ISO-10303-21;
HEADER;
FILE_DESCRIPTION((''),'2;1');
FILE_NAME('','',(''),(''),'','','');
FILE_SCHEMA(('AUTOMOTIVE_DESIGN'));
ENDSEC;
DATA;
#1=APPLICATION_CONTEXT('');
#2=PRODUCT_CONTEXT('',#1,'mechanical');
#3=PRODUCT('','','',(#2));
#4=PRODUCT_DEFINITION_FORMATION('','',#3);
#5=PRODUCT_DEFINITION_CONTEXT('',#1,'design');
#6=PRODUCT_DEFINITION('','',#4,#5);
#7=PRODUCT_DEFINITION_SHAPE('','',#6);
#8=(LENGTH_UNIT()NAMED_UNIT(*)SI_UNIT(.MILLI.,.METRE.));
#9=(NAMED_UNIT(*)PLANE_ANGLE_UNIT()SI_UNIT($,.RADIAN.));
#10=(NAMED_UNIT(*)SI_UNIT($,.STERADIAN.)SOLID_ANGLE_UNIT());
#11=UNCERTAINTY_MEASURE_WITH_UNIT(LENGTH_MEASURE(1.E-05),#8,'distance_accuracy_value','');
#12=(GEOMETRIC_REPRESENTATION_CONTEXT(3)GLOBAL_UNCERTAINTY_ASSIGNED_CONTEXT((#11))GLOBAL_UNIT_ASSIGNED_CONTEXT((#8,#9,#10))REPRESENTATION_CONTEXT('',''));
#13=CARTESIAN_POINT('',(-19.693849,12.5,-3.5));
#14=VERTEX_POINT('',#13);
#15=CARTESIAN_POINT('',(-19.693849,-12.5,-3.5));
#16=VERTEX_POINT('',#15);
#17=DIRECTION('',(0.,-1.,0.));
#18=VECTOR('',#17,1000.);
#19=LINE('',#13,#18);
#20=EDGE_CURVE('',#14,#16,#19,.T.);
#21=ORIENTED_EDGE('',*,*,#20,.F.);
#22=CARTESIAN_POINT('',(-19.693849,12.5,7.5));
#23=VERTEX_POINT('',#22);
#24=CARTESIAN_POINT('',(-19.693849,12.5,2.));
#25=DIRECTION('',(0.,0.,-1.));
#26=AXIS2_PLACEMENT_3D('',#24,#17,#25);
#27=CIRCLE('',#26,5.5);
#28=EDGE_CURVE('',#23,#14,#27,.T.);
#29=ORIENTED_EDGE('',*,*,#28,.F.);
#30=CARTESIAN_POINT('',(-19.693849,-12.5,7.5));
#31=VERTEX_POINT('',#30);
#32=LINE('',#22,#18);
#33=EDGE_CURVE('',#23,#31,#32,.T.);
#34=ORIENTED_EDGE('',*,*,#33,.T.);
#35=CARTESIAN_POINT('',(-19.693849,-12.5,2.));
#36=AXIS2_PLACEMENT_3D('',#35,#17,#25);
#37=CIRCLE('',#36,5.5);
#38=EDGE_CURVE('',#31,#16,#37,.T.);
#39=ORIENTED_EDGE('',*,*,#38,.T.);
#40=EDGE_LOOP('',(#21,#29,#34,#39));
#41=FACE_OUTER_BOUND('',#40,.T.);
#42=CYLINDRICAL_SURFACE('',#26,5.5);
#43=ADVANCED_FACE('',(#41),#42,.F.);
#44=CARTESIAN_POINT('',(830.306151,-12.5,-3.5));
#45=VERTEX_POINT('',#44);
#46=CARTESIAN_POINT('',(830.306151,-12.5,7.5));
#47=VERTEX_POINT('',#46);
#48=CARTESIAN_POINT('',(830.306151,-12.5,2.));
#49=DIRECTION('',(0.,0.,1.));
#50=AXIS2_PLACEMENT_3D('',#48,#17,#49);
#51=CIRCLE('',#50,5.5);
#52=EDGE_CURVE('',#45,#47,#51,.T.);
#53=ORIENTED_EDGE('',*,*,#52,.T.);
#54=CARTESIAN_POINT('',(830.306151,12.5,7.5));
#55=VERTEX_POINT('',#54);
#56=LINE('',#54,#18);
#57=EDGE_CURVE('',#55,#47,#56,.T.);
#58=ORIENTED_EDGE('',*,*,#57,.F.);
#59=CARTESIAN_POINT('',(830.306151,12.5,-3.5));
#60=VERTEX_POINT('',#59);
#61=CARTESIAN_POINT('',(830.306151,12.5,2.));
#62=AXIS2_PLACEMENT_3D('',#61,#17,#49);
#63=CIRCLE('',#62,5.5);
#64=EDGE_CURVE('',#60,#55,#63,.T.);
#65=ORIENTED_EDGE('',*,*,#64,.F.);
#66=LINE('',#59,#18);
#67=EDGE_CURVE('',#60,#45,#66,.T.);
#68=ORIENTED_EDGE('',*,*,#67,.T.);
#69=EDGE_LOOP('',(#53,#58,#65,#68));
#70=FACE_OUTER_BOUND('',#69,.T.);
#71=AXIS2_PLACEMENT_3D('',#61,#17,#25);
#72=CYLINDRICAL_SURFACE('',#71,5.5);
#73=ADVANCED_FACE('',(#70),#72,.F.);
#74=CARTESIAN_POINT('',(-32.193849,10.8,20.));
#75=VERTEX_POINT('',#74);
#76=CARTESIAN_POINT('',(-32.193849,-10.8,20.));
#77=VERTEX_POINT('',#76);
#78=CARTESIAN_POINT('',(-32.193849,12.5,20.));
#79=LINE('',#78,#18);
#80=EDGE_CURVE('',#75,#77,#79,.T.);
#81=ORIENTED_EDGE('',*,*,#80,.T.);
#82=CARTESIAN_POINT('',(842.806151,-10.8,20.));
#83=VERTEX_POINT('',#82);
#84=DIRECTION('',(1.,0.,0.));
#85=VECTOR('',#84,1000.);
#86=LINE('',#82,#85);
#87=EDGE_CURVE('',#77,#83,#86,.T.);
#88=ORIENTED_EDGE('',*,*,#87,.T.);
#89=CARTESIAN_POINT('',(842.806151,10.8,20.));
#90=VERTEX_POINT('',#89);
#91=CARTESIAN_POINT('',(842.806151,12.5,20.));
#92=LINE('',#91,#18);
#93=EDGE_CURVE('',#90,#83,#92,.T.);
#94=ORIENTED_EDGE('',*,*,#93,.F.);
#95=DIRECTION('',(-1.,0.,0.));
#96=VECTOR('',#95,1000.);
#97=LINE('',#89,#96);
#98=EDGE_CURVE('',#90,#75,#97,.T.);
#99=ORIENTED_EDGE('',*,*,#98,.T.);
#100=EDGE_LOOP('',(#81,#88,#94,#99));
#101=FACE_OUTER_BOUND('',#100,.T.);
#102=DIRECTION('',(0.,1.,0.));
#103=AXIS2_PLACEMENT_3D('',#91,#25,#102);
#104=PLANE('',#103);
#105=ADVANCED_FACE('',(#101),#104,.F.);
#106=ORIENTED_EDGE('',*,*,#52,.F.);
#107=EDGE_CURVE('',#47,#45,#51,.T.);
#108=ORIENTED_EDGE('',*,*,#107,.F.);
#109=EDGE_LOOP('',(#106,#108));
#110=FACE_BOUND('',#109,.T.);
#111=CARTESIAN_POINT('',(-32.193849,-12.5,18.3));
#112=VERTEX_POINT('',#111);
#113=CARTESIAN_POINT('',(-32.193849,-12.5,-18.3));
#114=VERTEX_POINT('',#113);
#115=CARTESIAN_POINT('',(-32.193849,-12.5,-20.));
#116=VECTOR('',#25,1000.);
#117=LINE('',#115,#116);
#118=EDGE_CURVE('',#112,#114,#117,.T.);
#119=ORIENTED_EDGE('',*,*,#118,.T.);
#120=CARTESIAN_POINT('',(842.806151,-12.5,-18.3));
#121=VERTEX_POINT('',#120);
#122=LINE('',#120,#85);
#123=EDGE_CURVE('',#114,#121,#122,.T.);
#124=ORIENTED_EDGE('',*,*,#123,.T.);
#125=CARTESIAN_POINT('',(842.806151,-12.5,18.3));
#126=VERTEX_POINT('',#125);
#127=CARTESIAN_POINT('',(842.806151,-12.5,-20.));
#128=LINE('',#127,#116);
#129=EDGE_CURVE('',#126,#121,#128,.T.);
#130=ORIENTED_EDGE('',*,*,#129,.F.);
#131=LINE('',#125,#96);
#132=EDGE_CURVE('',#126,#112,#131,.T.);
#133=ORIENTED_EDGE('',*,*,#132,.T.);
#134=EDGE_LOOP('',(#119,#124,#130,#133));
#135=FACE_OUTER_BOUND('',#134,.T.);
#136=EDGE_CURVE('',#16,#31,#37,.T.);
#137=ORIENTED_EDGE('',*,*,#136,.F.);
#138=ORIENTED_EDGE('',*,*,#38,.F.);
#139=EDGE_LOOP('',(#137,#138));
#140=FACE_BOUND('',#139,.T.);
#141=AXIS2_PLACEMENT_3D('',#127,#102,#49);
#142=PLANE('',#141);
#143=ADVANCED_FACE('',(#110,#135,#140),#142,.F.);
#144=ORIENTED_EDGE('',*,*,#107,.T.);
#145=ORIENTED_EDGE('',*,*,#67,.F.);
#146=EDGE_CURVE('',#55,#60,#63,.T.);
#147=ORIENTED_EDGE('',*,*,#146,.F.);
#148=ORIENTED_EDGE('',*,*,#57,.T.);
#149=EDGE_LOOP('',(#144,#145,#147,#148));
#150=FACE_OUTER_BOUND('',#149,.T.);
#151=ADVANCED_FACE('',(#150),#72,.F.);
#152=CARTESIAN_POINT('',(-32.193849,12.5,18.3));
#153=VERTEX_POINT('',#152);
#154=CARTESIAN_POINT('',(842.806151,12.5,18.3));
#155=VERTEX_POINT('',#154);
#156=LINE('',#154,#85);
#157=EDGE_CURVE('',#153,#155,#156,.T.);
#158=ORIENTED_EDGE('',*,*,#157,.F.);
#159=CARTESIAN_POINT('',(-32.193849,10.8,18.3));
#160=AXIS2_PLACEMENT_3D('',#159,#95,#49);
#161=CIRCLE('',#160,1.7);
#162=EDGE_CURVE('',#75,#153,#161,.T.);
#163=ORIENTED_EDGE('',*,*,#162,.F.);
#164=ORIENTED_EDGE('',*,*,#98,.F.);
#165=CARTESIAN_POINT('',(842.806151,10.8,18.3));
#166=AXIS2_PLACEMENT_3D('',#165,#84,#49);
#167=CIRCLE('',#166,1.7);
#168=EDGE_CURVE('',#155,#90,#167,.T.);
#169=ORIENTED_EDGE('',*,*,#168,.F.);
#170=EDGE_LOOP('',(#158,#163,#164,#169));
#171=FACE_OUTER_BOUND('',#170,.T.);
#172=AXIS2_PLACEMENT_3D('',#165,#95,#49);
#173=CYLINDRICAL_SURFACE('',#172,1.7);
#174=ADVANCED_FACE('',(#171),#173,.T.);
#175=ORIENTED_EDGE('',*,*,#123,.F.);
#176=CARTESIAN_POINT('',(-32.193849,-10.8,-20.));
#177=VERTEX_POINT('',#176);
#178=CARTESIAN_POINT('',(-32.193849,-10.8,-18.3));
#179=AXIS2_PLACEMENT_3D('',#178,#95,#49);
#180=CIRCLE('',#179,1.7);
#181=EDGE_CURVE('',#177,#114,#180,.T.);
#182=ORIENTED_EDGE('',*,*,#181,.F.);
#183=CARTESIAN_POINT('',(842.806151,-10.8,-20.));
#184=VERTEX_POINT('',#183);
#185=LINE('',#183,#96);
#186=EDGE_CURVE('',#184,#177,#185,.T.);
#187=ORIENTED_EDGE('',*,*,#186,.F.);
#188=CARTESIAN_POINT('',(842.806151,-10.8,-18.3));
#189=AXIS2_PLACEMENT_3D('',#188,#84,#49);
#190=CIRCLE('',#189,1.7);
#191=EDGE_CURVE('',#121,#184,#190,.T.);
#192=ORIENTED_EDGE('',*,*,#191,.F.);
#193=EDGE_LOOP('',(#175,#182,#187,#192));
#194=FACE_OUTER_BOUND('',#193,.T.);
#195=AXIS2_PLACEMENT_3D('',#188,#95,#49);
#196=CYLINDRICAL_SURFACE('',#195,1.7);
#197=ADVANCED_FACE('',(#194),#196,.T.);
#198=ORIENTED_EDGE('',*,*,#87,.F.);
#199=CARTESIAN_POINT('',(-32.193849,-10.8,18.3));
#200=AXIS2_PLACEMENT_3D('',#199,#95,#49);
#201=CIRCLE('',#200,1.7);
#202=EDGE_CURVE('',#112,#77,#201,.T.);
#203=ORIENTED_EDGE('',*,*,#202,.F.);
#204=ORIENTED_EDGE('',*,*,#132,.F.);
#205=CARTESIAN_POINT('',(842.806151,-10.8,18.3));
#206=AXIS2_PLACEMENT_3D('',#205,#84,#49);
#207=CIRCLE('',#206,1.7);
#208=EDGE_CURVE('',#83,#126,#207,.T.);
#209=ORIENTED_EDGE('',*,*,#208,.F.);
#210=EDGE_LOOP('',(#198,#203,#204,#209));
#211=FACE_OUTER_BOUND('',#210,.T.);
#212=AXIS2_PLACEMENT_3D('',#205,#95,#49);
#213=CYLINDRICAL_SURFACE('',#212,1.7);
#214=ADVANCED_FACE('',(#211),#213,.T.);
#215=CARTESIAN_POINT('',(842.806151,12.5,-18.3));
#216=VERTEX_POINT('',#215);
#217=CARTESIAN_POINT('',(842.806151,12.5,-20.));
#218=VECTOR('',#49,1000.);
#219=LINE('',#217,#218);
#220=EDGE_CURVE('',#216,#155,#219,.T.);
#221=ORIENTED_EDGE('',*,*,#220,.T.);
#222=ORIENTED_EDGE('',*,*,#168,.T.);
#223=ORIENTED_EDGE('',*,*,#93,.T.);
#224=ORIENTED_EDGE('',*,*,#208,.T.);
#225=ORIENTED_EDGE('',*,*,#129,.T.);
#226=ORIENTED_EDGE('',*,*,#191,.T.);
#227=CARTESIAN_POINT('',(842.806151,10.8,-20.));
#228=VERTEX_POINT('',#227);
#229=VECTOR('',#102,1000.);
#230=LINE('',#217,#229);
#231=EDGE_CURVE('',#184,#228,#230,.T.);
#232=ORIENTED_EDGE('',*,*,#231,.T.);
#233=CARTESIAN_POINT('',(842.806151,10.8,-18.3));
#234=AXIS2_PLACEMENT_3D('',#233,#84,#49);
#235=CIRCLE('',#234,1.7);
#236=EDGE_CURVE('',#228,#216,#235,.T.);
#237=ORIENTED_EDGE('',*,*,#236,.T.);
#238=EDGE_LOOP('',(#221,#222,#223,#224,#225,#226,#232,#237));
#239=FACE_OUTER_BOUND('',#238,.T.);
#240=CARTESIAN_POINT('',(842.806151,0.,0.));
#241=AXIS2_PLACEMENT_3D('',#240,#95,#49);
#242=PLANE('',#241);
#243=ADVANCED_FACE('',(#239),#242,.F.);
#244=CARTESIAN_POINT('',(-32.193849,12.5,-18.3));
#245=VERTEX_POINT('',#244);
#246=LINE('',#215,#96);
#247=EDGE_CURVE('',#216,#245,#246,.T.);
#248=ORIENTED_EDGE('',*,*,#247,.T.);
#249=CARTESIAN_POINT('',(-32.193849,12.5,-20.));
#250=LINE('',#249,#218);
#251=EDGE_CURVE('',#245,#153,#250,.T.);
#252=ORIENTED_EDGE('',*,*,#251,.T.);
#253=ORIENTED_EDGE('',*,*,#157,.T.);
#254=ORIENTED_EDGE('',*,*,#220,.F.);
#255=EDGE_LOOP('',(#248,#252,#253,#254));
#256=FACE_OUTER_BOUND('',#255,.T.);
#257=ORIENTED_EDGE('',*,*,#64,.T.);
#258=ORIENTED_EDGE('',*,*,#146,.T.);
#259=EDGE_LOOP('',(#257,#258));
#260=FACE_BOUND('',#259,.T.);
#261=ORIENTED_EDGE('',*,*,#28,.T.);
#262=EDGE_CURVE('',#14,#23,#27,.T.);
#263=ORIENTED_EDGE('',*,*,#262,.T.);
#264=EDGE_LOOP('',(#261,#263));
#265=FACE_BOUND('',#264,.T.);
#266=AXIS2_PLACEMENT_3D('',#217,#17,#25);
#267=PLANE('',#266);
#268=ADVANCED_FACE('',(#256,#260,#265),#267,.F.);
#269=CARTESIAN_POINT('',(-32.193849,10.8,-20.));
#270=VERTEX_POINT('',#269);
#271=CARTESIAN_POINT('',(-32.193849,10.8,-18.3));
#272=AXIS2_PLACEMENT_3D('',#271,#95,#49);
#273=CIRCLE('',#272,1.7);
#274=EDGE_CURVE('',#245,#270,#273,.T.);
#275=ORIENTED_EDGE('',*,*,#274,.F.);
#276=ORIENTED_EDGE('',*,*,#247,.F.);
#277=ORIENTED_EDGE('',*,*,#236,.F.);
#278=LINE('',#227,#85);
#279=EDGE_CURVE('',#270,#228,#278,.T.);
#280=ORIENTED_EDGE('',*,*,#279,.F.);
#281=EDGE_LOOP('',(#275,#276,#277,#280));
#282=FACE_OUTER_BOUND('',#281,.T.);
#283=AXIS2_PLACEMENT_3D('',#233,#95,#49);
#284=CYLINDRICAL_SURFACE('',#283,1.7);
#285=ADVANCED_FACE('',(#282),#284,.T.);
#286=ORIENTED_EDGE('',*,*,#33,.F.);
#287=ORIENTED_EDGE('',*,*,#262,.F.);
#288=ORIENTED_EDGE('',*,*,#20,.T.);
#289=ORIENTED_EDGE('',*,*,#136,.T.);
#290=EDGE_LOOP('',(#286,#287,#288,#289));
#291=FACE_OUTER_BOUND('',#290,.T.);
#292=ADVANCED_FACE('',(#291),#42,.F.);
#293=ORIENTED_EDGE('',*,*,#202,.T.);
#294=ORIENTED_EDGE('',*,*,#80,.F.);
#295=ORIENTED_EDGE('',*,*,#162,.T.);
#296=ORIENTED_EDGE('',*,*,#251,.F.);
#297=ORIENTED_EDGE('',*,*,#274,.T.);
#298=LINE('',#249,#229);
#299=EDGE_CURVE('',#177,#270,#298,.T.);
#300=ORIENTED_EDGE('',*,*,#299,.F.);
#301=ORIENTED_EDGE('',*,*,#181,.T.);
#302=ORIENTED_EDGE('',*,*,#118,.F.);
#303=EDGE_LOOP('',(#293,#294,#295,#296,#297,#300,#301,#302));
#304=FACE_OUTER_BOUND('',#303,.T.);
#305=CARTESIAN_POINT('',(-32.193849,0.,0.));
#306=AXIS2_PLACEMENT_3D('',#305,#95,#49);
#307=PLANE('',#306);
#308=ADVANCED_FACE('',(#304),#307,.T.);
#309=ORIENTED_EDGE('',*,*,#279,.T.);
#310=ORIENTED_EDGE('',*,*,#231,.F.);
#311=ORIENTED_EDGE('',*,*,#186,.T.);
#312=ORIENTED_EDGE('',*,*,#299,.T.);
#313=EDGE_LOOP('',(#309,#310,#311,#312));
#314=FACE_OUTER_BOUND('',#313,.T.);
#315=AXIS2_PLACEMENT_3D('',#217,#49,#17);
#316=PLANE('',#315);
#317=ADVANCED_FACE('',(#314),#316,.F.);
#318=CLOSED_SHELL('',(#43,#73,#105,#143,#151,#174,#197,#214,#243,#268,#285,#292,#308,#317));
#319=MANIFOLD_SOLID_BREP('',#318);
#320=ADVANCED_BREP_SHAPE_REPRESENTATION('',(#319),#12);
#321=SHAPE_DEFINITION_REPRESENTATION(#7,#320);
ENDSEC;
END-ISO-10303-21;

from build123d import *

# Parameters (mm, degrees)
SKETCH2_W          = 40
SKETCH2_H          = 25
FILLET1_R          = 1.7
SKETCH3_R          = 5.5
CUT_EXTRUDE1_DEPTH = 844.414019404


with BuildPart() as part:
    # Sweep1: sweep along a path in Sketch1
    with BuildLine(Plane.XY) as sweep1_path:
        Line((-32.193849021, 0), (842.806150979, 0))
    # Sketch2 → Sweep1 (sweep)
    with BuildSketch(Plane(origin=(-32.193849021, 0, 0), x_dir=(0, 0, -1), z_dir=(1, 0, 0))):
        Rectangle(SKETCH2_W, SKETCH2_H)
    sweep(path=sweep1_path.line)

    # Fillet1
    fillet1_edges = [part.edges().sort_by_distance(p)[0] for p in [
        (405.306150979, 12.5, 20),
        (405.306150979, 12.5, -20),
        (405.306150979, -12.5, -20),
        (405.306150979, -12.5, 20),
    ]]
    fillet(fillet1_edges, radius=FILLET1_R)

    # Sketch3 → Cut-Extrude1 (cut, through all)
    with BuildSketch(Plane(origin=(0, -12.5, 0), x_dir=(-1, 0, 0), z_dir=(0, -1, 0))):
        with Locations(Location((19.693849021, -2, 0), (0, 0, 90))):
            Circle(SKETCH3_R)
        with Locations(Location((-830.306150979, -2, 0), (0, 0, 270))):
            Circle(SKETCH3_R)
    extrude(amount=-CUT_EXTRUDE1_DEPTH, mode=Mode.SUBTRACT)


solid = part.part
